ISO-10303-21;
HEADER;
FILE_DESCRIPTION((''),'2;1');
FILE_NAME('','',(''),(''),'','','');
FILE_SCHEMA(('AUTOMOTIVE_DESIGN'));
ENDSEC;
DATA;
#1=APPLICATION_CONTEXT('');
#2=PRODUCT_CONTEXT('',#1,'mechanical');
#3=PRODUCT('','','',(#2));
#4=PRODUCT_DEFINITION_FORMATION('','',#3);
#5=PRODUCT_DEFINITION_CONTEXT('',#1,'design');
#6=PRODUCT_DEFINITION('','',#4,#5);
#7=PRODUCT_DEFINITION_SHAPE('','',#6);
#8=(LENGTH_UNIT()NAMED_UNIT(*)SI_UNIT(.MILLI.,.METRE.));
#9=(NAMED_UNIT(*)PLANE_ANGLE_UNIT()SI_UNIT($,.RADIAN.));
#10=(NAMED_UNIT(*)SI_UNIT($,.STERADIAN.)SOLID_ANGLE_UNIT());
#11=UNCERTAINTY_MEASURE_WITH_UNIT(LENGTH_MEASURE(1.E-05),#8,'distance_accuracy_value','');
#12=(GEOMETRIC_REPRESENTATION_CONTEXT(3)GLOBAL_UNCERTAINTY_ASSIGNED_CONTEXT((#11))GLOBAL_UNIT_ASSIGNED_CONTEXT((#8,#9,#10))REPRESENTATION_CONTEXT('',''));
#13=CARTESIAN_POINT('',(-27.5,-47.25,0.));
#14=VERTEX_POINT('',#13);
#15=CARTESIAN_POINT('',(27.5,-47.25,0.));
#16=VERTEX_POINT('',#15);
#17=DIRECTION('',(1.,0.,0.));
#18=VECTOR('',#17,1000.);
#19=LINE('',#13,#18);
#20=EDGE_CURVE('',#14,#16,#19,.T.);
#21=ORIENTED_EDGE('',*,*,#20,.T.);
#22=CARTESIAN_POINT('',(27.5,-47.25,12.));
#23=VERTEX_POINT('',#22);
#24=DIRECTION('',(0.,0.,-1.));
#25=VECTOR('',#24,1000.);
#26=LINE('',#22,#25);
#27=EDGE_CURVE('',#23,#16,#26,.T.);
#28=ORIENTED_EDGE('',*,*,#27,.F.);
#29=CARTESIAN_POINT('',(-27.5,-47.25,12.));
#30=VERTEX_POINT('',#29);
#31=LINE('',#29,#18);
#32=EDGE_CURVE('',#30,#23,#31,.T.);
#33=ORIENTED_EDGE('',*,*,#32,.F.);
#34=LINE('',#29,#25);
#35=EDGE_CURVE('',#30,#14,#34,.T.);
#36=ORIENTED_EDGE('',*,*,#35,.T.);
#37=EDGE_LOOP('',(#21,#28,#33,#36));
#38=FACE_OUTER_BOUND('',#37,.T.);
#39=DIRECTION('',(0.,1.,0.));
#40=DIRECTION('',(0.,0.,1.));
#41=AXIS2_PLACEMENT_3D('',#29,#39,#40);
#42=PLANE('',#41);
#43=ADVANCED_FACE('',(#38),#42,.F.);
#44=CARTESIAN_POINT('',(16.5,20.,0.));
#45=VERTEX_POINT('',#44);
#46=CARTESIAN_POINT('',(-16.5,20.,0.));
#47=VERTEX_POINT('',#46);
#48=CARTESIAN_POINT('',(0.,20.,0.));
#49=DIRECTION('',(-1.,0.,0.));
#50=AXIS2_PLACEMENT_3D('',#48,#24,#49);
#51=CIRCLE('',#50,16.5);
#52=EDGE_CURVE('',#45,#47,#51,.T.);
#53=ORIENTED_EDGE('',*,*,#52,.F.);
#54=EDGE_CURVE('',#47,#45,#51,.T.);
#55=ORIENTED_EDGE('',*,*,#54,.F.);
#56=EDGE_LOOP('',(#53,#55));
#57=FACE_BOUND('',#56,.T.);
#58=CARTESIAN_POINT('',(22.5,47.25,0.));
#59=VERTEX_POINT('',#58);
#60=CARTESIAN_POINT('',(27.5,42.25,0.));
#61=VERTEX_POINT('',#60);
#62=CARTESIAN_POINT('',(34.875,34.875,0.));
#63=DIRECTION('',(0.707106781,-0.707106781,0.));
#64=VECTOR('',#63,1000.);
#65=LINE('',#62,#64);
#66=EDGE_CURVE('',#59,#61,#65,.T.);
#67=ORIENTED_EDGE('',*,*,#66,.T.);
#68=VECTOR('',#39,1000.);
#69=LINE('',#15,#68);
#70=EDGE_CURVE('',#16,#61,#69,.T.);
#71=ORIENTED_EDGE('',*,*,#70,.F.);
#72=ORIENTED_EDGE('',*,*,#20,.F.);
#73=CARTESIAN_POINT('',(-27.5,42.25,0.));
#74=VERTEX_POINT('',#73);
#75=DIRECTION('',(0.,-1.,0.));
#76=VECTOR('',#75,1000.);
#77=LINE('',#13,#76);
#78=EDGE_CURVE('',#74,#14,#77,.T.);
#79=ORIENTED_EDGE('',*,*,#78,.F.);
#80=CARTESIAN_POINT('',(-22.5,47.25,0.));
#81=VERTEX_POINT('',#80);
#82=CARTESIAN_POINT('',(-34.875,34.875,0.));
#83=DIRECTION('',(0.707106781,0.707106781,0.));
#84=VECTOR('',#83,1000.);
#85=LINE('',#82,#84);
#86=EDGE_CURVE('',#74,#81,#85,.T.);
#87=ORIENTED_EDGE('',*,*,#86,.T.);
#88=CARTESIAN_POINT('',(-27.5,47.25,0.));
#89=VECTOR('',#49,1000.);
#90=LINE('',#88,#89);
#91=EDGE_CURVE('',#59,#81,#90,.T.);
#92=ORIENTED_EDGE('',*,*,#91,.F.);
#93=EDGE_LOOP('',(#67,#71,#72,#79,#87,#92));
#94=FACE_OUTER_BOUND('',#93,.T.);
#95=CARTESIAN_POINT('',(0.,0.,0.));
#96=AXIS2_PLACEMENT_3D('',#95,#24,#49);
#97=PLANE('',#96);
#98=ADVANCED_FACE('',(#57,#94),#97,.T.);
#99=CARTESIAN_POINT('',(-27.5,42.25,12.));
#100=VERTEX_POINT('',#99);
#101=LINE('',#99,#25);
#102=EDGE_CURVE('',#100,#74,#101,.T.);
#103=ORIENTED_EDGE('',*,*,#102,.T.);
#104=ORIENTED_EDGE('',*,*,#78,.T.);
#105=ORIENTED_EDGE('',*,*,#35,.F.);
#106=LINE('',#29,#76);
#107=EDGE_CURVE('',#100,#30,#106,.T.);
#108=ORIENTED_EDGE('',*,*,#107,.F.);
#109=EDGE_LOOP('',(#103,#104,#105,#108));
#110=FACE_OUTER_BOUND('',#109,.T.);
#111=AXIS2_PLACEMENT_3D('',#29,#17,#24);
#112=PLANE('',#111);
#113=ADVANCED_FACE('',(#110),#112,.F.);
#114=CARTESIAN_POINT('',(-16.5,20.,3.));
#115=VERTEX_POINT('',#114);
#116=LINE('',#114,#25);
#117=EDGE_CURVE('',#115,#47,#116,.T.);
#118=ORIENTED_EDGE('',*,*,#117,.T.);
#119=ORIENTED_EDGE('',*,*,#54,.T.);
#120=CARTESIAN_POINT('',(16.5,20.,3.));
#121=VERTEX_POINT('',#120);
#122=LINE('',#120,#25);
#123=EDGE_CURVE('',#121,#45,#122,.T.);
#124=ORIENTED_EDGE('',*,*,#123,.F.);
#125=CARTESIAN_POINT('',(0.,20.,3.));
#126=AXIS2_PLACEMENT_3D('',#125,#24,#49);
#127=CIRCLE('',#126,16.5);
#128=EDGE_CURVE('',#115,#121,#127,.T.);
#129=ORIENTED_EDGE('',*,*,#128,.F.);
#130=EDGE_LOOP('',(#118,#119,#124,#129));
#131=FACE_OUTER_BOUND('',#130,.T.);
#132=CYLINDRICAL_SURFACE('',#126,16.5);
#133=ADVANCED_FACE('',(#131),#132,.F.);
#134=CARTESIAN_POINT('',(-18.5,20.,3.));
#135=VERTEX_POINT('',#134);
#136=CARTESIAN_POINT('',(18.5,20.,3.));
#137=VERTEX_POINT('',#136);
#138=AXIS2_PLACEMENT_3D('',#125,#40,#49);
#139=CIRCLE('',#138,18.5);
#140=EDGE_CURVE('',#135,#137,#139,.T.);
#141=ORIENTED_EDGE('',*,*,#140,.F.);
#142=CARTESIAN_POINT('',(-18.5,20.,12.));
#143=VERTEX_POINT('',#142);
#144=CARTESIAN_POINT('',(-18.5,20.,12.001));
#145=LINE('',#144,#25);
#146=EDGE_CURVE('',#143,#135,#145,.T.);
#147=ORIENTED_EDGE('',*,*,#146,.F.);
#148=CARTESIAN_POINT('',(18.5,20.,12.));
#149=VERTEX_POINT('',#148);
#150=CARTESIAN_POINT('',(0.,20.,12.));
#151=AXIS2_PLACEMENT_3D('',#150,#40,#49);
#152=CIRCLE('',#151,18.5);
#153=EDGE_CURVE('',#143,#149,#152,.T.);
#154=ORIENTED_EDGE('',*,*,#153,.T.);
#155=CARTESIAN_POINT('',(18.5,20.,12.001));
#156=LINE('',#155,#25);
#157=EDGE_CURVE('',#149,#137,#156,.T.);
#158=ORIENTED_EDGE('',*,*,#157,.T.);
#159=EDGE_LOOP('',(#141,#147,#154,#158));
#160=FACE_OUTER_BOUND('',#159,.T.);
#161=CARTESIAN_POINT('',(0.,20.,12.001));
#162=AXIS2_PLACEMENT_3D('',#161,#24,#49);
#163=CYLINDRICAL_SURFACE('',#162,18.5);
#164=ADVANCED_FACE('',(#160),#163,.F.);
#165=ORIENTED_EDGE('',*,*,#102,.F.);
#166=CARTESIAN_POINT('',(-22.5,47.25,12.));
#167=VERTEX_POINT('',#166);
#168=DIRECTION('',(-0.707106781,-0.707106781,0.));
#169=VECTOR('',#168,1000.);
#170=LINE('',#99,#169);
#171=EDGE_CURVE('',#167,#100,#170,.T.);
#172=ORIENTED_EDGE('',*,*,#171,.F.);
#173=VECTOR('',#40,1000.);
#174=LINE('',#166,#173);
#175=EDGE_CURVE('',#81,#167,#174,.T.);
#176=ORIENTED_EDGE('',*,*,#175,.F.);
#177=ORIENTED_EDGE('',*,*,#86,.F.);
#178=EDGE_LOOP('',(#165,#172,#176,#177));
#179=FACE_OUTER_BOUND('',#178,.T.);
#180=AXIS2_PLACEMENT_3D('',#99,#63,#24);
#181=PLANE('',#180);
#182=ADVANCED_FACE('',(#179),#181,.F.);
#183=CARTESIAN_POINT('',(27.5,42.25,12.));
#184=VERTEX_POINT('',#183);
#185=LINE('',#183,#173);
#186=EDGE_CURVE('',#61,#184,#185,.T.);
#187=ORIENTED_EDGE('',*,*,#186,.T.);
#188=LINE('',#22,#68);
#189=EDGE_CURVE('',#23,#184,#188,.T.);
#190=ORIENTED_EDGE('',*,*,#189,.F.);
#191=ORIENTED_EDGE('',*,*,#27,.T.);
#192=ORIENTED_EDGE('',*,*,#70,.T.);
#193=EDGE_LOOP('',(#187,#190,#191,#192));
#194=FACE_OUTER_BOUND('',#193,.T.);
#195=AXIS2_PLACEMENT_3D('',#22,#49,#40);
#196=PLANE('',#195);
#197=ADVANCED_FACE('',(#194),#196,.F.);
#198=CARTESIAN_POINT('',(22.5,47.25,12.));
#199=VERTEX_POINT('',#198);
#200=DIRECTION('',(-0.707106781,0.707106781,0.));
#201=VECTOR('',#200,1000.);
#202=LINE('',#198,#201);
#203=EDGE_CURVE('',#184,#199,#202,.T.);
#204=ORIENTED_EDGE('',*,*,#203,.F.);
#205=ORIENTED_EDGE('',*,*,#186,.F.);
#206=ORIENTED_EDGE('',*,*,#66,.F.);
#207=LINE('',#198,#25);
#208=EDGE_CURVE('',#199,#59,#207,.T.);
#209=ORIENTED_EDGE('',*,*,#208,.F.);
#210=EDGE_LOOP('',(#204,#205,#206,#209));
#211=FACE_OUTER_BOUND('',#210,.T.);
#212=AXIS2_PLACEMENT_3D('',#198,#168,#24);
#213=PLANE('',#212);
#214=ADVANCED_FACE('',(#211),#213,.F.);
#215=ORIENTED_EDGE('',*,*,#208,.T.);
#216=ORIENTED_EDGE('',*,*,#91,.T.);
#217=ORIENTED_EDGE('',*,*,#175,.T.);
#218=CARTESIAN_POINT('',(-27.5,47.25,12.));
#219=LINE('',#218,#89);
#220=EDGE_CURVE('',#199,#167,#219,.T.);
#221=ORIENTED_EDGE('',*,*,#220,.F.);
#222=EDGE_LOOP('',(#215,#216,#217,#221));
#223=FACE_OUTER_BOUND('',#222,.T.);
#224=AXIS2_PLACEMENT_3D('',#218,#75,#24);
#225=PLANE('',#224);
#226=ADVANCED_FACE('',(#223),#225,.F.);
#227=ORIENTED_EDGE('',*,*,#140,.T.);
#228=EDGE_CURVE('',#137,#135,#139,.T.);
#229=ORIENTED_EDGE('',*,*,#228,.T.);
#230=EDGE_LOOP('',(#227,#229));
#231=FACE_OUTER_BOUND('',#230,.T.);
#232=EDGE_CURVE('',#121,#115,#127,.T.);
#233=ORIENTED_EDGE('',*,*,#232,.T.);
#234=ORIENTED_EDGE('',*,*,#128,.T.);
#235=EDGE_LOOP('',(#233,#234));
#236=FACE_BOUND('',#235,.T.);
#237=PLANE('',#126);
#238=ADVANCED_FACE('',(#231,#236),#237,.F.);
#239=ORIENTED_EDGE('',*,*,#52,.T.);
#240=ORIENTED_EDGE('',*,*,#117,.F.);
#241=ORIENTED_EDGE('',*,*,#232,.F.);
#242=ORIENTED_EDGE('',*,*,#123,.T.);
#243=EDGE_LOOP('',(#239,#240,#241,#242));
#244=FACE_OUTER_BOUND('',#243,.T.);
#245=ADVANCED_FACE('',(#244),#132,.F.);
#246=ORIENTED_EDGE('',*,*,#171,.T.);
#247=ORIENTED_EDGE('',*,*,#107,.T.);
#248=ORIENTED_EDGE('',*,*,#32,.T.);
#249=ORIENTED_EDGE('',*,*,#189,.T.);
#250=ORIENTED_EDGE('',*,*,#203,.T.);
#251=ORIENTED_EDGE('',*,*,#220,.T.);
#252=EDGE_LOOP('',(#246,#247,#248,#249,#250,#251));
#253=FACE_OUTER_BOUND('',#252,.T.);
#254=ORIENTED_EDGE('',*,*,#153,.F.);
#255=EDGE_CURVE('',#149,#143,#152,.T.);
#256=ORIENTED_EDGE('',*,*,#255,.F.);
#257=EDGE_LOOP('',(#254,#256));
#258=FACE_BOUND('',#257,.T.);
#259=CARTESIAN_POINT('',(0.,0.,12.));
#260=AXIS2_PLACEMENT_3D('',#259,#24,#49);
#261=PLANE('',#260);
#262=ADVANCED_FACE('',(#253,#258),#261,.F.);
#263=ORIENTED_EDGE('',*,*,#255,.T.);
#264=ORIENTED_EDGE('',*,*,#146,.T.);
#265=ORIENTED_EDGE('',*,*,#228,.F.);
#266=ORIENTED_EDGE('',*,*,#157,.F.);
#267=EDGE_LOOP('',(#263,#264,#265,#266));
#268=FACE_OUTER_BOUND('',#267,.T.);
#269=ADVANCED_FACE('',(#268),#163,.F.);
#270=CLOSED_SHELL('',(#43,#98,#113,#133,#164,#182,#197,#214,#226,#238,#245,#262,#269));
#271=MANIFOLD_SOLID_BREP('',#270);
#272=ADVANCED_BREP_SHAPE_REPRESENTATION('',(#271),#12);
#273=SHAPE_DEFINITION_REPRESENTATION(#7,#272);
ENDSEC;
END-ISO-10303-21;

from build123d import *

# Parameters (mm, degrees)
SKETCH_1_W          = 55
SKETCH_1_H          = 94.5
EXTRUDE_1_DEPTH     = 12
CUT_EXTRUDE_4_REACH = 57.972
SKETCH_5_R          = 18.5
CHAMFER_1_SIZE      = 5
SKETCH_6_R          = 18.5
SKETCH_6_R_2        = 16.5
EXTRUDE_2_DEPTH     = 3


with BuildPart() as part:
    # 草图1 → 凸台-拉伸1 (new body)
    with BuildSketch(Plane.XY):
        Rectangle(SKETCH_1_W, SKETCH_1_H)
    extrude(amount=EXTRUDE_1_DEPTH)

    # 草图5 → 切除-拉伸4 (cut, up to next)
    with BuildSketch(Plane(origin=(0, 0, 0), x_dir=(-1, 0, 0), z_dir=(0, 0, -1)), mode=Mode.PRIVATE) as cut_extrude_4_sk1:
        with Locations((0, 20)):
            Circle(SKETCH_5_R)
    cut_extrude_4_tool1 = extrude(cut_extrude_4_sk1.sketch, amount=-CUT_EXTRUDE_4_REACH, mode=Mode.PRIVATE) & part.part
    add(cut_extrude_4_tool1.solids().sort_by_distance((0, 20, 0))[0], mode=Mode.SUBTRACT)

    # 倒角1
    chamfer_1_edges = [part.edges().sort_by_distance(p)[0] for p in [
        (-27.5, 47.25, 6),
        (27.5, 47.25, 6),
    ]]
    chamfer(chamfer_1_edges, length=CHAMFER_1_SIZE)

    # 草图6 → 凸台-拉伸2 (add)
    with BuildSketch(Plane(origin=(0, 0, 0), x_dir=(-1, 0, 0), z_dir=(0, 0, -1))):
        with Locations((0, 20)):
            Circle(SKETCH_6_R)
        with Locations((0, 20)):
            Circle(SKETCH_6_R_2, mode=Mode.SUBTRACT)
    extrude(amount=-EXTRUDE_2_DEPTH)


solid = part.part
